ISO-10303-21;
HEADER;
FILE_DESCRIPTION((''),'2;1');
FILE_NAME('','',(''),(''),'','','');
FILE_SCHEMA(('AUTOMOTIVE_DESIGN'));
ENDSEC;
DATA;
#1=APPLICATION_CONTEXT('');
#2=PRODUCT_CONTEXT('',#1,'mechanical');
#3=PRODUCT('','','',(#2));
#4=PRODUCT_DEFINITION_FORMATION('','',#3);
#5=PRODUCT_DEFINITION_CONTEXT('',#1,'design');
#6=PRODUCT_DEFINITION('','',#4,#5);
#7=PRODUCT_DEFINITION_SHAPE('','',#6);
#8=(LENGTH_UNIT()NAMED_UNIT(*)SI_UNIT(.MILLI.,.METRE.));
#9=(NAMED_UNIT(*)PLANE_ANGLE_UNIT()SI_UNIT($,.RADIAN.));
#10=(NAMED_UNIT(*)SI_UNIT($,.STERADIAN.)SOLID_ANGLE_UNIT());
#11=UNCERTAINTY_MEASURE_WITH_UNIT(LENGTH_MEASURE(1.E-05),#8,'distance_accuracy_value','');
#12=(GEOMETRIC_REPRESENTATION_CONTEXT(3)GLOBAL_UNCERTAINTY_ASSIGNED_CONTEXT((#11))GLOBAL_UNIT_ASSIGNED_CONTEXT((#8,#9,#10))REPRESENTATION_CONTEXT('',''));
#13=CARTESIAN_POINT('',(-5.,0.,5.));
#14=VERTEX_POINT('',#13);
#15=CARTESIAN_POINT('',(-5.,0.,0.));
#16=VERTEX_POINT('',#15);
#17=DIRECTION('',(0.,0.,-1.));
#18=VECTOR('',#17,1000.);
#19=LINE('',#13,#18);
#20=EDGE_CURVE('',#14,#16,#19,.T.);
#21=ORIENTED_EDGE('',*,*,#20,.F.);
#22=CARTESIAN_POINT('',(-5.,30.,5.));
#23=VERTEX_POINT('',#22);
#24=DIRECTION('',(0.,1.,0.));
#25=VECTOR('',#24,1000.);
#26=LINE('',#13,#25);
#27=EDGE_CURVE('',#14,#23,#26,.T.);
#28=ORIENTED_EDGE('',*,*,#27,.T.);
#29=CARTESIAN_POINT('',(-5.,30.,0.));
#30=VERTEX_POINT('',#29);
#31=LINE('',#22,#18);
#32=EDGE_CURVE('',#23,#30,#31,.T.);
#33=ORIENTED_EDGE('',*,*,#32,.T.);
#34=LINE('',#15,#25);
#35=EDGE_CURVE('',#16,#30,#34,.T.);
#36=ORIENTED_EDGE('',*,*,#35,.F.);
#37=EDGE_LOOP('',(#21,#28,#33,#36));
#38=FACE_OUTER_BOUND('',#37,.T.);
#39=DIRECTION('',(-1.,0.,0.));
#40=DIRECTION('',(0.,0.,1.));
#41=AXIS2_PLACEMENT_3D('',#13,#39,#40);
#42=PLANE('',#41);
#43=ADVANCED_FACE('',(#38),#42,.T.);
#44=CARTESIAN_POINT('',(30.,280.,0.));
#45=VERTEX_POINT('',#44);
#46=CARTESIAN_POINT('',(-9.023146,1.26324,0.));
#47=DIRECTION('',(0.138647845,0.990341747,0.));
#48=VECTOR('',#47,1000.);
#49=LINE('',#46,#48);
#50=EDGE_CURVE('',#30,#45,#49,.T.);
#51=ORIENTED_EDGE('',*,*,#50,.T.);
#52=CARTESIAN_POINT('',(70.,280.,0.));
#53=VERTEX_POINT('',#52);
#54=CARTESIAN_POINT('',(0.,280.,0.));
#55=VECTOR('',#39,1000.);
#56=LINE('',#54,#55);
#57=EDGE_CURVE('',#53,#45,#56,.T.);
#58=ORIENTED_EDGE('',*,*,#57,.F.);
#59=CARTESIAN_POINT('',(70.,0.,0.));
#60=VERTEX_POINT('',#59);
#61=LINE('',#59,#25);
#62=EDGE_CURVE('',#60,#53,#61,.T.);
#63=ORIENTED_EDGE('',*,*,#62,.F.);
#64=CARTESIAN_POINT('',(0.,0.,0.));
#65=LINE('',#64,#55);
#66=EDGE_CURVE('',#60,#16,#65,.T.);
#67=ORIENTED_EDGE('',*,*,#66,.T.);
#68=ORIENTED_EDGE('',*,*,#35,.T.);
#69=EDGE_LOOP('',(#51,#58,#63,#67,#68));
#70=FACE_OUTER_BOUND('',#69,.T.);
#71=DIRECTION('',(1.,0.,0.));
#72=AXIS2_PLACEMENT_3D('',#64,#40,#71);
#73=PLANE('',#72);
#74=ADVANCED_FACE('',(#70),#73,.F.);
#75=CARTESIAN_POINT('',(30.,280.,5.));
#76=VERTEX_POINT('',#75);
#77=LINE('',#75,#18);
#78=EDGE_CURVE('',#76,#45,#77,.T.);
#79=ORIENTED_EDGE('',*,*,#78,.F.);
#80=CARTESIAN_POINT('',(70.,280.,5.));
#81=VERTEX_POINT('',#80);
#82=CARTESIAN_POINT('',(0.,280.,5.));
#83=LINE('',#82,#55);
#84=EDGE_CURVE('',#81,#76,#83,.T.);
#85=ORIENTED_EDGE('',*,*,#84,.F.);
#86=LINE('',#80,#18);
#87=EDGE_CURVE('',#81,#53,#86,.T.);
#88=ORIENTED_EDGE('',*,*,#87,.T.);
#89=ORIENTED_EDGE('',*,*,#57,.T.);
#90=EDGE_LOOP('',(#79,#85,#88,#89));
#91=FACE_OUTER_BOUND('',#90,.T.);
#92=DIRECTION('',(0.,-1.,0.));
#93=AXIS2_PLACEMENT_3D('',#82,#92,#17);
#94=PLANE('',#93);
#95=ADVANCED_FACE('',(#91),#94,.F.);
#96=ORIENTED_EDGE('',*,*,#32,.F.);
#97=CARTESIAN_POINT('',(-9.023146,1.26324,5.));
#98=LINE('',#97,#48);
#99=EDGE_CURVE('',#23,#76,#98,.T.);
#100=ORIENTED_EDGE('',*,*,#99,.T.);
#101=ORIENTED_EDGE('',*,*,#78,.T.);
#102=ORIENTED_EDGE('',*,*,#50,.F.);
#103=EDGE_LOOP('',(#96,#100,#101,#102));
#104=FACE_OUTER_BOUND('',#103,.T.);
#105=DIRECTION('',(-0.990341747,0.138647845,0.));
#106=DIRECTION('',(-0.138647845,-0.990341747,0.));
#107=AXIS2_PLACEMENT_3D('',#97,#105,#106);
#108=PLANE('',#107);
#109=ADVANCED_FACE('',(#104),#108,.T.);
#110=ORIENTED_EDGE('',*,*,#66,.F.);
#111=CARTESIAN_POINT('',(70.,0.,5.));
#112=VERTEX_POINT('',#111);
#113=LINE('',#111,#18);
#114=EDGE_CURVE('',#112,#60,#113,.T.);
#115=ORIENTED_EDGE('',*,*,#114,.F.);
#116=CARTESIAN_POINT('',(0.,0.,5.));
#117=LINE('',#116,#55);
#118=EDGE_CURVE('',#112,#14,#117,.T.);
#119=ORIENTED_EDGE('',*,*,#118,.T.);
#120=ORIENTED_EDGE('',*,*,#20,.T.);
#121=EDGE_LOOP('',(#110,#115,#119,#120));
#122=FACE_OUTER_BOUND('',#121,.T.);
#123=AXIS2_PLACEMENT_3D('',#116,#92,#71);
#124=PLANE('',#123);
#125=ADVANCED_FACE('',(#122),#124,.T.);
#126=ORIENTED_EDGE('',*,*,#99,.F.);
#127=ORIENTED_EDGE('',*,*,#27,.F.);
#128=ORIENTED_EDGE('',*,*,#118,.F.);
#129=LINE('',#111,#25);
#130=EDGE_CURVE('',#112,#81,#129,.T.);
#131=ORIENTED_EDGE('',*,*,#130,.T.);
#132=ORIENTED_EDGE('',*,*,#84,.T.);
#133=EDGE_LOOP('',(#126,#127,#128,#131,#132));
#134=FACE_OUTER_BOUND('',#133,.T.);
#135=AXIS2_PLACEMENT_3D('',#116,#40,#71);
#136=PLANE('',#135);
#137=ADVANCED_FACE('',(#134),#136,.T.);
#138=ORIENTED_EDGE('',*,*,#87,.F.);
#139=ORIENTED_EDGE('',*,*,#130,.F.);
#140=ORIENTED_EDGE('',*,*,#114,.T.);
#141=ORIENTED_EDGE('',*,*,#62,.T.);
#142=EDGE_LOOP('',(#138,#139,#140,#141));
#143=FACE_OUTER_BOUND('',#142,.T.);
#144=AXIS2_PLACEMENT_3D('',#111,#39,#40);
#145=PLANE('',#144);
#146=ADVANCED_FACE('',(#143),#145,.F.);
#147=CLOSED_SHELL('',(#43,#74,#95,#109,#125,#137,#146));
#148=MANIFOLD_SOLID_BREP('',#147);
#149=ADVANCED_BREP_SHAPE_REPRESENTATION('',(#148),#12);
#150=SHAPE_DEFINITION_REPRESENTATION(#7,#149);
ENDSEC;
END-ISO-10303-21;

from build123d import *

# Parameters (mm, degrees)
EXTRUDE_3_DEPTH = 5


with BuildPart() as part:
    # 草图1 → 凸台-拉伸3 (new body)
    with BuildSketch(Plane.XY):
        Polygon((-5, 0), (0, 0), (70, 0), (70, 280), (30, 280), (-5, 30), align=None)
    extrude(amount=EXTRUDE_3_DEPTH)


solid = part.part
